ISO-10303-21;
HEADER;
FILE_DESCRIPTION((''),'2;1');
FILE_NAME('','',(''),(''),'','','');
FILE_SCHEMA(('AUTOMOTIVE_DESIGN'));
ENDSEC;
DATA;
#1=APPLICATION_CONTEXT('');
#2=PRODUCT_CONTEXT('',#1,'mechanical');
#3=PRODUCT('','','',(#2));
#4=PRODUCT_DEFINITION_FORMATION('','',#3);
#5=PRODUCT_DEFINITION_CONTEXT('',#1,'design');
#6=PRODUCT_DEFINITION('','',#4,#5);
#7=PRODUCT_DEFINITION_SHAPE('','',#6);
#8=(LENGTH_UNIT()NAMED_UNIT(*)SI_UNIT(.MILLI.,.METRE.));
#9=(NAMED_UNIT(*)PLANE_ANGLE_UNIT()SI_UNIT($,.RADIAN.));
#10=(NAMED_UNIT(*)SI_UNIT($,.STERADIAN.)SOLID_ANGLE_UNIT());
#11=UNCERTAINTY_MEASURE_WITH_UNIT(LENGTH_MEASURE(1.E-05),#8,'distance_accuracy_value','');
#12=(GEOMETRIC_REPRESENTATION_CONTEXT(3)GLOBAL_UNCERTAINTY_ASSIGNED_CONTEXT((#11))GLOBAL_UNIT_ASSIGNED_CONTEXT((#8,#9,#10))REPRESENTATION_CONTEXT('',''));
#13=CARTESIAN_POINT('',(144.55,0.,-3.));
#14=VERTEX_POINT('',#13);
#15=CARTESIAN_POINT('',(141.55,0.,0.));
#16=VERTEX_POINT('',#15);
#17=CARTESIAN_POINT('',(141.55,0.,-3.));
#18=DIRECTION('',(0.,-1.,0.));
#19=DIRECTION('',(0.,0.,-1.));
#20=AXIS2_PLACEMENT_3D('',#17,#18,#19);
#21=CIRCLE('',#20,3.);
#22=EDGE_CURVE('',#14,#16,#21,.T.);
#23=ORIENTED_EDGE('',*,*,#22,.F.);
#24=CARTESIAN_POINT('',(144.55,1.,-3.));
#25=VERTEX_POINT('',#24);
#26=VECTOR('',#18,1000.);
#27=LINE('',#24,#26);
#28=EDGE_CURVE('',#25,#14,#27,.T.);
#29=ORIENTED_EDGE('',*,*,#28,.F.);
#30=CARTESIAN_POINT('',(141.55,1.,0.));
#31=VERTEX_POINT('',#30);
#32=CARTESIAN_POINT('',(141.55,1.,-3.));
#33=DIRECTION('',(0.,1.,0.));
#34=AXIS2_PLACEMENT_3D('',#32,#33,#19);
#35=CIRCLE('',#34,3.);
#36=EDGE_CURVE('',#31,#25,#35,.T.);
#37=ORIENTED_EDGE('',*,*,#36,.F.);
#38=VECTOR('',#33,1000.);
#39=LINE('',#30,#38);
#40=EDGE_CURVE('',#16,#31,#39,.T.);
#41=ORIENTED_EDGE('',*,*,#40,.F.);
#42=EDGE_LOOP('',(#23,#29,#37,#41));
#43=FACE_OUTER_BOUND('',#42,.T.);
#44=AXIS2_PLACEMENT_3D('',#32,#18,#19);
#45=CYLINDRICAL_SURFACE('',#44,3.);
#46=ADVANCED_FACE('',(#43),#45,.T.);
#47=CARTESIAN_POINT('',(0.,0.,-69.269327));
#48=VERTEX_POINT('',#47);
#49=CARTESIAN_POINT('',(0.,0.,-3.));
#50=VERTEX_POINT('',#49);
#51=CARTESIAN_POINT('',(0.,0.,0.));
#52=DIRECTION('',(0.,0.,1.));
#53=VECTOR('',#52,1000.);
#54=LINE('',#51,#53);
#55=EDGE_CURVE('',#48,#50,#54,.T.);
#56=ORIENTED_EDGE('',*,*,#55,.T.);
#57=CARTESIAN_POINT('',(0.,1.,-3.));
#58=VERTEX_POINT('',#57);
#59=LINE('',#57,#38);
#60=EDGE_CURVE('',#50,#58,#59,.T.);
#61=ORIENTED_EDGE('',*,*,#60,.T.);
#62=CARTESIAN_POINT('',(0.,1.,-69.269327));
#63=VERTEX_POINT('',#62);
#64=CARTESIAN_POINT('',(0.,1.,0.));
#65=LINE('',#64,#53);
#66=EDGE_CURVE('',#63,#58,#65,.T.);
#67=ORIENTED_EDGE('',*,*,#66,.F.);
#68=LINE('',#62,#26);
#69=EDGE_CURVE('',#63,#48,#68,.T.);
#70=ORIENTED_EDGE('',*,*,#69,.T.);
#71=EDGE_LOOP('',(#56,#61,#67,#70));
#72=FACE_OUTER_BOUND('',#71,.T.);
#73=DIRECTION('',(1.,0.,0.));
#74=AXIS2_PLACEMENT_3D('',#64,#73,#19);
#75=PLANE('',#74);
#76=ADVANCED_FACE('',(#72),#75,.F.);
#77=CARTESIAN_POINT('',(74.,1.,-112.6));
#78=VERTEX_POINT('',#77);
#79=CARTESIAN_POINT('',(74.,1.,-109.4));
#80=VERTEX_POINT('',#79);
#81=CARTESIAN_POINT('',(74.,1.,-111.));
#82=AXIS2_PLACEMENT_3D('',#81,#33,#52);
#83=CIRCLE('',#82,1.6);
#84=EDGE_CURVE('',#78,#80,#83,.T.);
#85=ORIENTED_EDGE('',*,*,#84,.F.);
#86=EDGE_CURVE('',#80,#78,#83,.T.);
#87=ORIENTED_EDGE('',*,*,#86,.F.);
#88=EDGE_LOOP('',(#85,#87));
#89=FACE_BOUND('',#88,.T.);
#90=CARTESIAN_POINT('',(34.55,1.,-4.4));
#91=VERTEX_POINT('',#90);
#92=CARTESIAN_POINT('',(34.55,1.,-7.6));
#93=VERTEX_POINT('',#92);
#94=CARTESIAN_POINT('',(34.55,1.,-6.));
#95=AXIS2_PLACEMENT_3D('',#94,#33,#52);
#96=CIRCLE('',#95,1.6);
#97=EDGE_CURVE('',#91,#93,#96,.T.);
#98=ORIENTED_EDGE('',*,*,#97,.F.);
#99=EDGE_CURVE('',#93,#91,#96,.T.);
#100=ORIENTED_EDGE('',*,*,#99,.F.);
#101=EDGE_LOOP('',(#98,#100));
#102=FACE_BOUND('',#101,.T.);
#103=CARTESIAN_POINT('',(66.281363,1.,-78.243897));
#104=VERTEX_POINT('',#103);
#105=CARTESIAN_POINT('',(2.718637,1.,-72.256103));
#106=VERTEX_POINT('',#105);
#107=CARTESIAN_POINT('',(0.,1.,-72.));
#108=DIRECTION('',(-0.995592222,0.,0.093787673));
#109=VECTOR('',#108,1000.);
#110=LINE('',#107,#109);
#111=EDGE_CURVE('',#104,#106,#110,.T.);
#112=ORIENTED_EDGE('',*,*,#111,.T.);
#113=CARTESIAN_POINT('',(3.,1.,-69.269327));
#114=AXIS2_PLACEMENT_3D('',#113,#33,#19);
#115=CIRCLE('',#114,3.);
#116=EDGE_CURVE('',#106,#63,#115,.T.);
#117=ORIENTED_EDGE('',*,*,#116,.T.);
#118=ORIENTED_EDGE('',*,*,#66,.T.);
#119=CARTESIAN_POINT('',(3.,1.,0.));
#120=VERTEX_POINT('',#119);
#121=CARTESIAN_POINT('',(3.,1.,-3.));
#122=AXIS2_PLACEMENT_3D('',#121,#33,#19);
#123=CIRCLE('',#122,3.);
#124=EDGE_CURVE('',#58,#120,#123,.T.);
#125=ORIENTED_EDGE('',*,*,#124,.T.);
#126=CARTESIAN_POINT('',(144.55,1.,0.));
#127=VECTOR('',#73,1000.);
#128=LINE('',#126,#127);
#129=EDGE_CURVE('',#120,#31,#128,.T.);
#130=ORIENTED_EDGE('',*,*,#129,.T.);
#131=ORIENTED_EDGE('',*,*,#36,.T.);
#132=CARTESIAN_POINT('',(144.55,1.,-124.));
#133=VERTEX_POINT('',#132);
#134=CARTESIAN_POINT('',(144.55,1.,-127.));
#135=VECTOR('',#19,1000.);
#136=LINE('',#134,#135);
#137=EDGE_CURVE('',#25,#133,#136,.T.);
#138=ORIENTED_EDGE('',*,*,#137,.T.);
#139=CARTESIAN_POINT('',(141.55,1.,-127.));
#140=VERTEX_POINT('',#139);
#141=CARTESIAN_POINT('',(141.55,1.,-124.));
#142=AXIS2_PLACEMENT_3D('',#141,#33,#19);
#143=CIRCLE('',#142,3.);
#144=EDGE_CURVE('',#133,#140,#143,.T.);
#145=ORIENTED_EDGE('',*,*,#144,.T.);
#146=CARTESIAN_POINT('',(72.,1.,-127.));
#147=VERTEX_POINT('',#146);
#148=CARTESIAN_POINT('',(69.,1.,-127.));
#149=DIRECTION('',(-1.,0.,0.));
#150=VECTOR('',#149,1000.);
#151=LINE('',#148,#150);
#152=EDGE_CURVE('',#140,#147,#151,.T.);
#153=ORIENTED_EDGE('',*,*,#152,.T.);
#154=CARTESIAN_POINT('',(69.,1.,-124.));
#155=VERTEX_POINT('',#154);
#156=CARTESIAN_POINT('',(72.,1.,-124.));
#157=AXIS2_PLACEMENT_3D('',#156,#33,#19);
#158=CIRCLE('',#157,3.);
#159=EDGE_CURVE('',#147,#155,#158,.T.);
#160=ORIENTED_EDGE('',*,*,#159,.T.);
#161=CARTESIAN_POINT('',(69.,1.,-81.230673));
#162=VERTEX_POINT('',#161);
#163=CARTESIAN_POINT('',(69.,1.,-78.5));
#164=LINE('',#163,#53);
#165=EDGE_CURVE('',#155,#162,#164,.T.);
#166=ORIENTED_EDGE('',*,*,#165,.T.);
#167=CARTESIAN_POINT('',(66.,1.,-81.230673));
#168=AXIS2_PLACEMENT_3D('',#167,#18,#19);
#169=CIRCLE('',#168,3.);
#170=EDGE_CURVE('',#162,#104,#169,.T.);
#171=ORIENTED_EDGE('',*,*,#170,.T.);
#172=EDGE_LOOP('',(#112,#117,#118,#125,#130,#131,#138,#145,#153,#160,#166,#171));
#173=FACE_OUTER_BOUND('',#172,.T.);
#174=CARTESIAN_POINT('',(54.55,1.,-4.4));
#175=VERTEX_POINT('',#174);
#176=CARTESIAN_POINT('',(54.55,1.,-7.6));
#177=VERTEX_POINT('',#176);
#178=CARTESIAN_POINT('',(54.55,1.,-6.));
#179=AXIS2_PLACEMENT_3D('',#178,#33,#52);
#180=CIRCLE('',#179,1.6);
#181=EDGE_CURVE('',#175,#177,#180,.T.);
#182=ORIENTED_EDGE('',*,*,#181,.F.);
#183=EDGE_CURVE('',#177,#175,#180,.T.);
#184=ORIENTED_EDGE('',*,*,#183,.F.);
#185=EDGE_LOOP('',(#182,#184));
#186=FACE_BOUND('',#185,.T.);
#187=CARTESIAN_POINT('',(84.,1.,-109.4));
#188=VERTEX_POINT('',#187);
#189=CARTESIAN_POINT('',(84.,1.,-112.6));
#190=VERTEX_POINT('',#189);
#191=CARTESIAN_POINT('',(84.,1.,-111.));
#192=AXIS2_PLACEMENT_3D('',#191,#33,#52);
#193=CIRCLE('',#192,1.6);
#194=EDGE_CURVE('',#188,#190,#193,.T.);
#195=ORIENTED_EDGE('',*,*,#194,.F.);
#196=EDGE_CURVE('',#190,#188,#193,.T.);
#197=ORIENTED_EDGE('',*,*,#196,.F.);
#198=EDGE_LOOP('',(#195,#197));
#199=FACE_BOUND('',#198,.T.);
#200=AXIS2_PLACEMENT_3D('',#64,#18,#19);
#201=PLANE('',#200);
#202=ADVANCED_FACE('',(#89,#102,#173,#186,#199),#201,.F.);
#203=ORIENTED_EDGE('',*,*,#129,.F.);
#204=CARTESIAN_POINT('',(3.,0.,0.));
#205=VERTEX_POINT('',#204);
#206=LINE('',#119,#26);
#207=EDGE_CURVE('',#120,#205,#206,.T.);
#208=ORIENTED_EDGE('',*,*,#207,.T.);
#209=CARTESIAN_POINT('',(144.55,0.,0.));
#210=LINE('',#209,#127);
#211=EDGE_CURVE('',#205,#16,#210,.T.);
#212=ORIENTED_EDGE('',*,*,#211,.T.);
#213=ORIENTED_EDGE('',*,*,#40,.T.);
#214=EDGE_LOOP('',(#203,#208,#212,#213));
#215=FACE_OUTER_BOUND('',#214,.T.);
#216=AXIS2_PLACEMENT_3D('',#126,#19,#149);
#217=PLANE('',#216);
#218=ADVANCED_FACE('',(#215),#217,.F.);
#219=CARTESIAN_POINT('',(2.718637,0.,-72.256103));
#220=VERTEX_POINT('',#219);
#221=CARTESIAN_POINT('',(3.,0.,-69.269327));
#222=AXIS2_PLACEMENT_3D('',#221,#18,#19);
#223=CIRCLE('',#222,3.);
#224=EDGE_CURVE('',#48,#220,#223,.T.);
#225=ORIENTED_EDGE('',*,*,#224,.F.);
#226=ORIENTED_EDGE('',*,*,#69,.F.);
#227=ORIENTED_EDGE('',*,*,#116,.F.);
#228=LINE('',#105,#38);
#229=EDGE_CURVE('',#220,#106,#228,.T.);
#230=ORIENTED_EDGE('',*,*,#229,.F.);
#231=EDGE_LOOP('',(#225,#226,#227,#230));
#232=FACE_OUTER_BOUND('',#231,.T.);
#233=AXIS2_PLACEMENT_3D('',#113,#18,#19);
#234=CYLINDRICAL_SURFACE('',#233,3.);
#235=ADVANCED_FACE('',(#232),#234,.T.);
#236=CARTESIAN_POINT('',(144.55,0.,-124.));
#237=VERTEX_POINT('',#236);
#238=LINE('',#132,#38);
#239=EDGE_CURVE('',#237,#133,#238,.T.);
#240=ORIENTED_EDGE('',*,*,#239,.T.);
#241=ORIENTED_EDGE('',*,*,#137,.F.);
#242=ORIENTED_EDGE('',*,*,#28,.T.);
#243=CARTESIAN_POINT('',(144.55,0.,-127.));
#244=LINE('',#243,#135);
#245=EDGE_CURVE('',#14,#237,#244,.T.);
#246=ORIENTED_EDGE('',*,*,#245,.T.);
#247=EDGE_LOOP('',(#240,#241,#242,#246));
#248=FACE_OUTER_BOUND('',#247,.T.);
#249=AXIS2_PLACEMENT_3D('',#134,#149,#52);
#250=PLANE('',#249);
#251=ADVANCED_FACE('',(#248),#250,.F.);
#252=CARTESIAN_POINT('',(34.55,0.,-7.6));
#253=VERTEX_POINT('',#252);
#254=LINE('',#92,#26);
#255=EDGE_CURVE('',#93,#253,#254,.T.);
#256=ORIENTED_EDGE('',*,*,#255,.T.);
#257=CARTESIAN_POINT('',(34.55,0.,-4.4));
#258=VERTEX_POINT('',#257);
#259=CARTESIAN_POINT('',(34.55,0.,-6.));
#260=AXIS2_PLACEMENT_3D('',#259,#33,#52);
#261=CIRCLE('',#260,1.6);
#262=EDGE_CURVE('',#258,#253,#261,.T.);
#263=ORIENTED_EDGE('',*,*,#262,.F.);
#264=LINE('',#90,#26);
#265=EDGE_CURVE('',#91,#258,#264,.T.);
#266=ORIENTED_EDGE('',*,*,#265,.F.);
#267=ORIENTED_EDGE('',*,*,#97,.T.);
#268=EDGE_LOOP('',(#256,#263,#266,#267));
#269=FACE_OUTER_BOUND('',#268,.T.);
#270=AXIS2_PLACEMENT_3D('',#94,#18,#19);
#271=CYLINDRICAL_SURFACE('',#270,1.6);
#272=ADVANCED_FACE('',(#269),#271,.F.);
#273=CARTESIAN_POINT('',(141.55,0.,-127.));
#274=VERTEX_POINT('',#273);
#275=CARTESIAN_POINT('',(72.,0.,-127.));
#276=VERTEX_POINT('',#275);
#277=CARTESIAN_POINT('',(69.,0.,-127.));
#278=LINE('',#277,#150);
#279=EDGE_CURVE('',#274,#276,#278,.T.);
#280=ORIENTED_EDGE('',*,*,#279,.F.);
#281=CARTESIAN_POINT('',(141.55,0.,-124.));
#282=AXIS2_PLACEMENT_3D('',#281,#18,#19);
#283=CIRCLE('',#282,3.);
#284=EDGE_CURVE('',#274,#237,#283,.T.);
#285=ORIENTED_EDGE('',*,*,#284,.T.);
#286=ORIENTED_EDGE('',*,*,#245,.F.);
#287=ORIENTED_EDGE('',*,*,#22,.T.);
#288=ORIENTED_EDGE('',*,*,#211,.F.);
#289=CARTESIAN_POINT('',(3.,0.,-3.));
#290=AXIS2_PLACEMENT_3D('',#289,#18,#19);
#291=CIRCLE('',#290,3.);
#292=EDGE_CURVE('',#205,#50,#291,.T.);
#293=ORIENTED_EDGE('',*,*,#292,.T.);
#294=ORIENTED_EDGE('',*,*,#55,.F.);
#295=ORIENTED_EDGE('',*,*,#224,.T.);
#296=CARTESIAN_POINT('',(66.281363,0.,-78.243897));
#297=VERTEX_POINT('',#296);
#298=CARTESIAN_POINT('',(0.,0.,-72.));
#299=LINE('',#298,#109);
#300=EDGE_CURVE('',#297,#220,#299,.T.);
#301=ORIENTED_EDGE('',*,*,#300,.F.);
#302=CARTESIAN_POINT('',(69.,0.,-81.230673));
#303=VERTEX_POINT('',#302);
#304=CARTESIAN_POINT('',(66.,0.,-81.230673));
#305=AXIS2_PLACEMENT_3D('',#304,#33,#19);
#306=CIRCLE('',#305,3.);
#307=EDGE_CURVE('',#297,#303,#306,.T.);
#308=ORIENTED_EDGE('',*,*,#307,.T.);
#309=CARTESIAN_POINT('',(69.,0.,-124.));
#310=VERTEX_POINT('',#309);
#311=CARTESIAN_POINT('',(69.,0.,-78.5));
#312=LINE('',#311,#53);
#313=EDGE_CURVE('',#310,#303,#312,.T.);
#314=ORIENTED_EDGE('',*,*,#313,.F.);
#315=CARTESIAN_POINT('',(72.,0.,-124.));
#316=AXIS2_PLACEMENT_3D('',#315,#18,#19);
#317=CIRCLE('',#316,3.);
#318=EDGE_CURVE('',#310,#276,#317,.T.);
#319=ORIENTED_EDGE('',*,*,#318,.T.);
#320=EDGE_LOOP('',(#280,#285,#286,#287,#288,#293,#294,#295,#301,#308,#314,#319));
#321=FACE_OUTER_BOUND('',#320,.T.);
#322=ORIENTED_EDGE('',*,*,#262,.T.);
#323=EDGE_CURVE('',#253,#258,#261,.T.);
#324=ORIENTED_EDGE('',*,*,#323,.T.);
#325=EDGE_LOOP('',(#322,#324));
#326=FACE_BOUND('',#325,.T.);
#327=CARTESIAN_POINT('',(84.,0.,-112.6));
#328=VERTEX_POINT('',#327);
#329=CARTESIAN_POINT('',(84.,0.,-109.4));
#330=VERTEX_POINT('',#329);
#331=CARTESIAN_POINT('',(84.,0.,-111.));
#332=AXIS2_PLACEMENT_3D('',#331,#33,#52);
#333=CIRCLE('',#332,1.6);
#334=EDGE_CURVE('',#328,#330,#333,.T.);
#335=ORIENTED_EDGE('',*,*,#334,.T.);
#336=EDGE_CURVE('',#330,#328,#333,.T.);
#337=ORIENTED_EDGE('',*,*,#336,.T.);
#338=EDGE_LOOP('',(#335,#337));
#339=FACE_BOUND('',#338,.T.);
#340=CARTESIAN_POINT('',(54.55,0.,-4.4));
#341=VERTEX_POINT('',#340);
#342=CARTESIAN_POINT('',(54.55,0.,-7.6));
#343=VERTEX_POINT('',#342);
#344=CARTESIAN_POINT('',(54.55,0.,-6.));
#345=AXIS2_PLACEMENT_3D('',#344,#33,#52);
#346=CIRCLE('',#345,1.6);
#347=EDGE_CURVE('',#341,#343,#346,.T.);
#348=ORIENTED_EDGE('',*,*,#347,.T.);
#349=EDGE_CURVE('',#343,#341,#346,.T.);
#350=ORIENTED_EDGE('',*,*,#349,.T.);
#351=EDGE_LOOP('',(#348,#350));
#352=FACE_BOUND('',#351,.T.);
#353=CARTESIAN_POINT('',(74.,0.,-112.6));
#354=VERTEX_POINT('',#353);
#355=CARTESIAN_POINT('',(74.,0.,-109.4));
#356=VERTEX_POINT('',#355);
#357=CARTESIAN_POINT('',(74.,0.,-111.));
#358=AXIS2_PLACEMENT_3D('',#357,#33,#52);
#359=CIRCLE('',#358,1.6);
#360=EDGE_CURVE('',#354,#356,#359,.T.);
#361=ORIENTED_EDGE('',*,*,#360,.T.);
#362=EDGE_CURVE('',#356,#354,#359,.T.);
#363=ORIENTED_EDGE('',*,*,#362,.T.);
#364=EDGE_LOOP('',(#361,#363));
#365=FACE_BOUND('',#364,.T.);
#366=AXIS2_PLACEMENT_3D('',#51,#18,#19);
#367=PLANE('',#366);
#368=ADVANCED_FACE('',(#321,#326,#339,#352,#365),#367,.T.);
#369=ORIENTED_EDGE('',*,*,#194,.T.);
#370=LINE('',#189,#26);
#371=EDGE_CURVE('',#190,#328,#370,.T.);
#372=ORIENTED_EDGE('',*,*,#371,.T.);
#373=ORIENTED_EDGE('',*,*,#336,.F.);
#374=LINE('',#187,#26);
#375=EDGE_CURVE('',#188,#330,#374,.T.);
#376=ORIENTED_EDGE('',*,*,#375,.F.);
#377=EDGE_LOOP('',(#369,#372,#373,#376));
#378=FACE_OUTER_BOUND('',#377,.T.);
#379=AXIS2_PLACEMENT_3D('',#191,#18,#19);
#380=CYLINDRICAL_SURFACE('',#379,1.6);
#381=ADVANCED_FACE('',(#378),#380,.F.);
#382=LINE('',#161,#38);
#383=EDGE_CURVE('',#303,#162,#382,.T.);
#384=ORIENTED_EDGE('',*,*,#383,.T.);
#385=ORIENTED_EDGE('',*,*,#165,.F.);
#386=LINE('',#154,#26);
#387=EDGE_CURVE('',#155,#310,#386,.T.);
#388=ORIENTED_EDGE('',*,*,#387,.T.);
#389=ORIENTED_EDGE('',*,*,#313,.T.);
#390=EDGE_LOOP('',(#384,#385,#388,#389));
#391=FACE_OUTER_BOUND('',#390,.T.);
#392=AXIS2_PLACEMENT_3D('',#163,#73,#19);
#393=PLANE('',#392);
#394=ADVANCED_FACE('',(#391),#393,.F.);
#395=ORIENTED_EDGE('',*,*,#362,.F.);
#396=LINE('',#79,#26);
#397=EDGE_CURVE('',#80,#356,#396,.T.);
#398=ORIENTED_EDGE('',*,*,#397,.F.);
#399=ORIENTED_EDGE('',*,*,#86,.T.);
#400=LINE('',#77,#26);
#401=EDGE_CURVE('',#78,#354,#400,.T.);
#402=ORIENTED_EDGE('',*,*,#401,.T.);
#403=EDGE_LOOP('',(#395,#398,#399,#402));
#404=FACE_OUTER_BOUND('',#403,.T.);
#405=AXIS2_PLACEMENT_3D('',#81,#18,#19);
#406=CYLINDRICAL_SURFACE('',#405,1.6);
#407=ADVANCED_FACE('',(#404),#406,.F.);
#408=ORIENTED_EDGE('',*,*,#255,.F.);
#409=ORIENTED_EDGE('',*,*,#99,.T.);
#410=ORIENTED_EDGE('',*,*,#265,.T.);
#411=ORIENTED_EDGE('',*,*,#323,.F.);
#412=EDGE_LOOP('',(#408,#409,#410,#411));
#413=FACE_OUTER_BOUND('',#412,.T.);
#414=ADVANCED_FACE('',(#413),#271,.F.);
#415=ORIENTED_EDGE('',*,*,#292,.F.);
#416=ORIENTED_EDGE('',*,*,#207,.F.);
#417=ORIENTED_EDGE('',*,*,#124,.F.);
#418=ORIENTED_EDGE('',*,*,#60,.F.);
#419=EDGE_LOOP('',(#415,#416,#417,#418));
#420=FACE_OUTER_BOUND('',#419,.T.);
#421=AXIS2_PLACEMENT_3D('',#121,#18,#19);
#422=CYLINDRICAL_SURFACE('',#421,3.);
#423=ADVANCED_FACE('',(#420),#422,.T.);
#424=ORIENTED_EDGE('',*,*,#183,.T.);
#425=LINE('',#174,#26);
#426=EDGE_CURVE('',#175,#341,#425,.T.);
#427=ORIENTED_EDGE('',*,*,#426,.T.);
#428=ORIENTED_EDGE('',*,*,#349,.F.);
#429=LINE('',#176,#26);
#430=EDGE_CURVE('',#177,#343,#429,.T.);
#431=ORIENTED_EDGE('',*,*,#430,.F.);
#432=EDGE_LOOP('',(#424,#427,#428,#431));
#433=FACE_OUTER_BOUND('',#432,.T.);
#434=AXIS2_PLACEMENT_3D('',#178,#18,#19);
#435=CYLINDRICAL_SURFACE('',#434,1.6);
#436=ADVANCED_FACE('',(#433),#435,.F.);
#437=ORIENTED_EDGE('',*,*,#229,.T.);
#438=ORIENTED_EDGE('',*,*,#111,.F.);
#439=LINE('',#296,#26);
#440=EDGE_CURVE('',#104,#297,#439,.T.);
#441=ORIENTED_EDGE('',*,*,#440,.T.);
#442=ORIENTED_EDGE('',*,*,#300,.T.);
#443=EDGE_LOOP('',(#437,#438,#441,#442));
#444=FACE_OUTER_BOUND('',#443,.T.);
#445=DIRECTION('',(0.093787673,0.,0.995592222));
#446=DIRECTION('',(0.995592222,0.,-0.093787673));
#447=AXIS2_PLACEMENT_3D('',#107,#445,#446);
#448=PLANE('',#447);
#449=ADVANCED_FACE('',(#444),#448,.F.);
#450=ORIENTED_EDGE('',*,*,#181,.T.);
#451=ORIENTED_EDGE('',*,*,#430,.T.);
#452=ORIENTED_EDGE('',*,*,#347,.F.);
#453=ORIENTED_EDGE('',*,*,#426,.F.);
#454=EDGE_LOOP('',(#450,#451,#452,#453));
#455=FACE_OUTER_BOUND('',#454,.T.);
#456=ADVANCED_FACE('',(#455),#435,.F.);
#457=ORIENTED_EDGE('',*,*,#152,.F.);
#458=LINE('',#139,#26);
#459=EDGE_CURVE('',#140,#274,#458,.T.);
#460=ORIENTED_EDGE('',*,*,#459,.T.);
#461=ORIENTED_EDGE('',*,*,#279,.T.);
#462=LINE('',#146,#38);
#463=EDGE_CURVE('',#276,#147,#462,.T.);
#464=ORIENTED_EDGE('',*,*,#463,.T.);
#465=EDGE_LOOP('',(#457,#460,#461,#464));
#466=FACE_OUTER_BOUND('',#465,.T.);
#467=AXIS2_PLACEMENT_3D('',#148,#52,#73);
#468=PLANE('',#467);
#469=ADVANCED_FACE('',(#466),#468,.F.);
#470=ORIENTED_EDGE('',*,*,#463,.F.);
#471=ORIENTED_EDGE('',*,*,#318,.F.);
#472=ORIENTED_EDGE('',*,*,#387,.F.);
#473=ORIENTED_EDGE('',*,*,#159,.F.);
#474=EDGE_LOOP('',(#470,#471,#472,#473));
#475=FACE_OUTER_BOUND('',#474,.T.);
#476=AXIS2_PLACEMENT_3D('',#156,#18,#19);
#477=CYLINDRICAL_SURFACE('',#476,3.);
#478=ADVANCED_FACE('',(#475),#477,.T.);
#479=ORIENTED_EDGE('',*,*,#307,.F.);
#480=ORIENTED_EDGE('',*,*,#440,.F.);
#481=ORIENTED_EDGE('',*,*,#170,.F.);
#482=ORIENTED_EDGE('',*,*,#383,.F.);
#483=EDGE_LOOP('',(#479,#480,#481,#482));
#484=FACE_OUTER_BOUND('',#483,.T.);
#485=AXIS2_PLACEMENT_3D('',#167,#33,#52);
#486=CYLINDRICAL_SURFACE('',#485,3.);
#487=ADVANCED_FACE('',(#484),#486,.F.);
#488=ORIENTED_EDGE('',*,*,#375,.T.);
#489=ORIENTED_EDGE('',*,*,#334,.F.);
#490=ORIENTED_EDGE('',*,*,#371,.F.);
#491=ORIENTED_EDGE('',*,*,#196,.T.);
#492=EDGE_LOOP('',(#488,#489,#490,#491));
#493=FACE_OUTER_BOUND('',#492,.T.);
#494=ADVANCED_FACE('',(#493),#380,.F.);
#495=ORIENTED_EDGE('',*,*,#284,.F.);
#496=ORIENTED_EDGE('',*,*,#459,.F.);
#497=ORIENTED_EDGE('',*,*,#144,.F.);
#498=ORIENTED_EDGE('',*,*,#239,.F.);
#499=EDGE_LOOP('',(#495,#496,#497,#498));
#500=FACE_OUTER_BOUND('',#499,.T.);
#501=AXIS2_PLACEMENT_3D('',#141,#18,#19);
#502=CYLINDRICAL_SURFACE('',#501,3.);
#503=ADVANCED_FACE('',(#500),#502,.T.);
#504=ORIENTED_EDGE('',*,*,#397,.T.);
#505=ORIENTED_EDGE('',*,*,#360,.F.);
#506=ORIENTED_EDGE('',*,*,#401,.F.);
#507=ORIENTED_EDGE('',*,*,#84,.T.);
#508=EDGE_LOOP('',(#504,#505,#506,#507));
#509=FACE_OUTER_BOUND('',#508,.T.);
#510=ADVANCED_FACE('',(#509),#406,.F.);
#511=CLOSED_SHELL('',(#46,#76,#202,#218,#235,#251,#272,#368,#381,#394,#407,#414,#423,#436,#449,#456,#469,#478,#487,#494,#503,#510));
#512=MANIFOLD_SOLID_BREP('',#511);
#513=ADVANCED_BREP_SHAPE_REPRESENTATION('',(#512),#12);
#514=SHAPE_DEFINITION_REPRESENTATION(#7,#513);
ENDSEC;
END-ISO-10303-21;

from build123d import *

# Parameters (mm, degrees)
SKETCH_1_R      = 1.6
EXTRUDE_1_DEPTH = 1
FILLET_1_R      = 3


with BuildPart() as part:
    # 草图1 → 凸台-拉伸1 (new body)
    with BuildSketch(Plane(origin=(0, 0, 0), x_dir=(1, 0, 0), z_dir=(0, 1, 0))):
        Polygon((0, 0), (0, 72), (69, 78.5), (69, 127), (144.55, 127), (144.55, 0), align=None)
        with Locations(Location((74, 111, 0), (0, 0, 270))):
            Circle(SKETCH_1_R, mode=Mode.SUBTRACT)
        with Locations(Location((84, 111, 0), (0, 0, 270))):
            Circle(SKETCH_1_R, mode=Mode.SUBTRACT)
        with Locations(Location((34.55, 6, 0), (0, 0, 270))):
            Circle(SKETCH_1_R, mode=Mode.SUBTRACT)
        with Locations(Location((54.55, 6, 0), (0, 0, 270))):
            Circle(SKETCH_1_R, mode=Mode.SUBTRACT)
    extrude(amount=EXTRUDE_1_DEPTH)

    # 圆角1
    fillet_1_edges = [part.edges().sort_by_distance(p)[0] for p in [
        (0, 0.5, 0),
        (0, 0.5, -72),
        (69, 0.5, -78.5),
        (69, 0.5, -127),
        (144.55, 0.5, -127),
        (144.55, 0.5, 0),
    ]]
    fillet(fillet_1_edges, radius=FILLET_1_R)


solid = part.part
